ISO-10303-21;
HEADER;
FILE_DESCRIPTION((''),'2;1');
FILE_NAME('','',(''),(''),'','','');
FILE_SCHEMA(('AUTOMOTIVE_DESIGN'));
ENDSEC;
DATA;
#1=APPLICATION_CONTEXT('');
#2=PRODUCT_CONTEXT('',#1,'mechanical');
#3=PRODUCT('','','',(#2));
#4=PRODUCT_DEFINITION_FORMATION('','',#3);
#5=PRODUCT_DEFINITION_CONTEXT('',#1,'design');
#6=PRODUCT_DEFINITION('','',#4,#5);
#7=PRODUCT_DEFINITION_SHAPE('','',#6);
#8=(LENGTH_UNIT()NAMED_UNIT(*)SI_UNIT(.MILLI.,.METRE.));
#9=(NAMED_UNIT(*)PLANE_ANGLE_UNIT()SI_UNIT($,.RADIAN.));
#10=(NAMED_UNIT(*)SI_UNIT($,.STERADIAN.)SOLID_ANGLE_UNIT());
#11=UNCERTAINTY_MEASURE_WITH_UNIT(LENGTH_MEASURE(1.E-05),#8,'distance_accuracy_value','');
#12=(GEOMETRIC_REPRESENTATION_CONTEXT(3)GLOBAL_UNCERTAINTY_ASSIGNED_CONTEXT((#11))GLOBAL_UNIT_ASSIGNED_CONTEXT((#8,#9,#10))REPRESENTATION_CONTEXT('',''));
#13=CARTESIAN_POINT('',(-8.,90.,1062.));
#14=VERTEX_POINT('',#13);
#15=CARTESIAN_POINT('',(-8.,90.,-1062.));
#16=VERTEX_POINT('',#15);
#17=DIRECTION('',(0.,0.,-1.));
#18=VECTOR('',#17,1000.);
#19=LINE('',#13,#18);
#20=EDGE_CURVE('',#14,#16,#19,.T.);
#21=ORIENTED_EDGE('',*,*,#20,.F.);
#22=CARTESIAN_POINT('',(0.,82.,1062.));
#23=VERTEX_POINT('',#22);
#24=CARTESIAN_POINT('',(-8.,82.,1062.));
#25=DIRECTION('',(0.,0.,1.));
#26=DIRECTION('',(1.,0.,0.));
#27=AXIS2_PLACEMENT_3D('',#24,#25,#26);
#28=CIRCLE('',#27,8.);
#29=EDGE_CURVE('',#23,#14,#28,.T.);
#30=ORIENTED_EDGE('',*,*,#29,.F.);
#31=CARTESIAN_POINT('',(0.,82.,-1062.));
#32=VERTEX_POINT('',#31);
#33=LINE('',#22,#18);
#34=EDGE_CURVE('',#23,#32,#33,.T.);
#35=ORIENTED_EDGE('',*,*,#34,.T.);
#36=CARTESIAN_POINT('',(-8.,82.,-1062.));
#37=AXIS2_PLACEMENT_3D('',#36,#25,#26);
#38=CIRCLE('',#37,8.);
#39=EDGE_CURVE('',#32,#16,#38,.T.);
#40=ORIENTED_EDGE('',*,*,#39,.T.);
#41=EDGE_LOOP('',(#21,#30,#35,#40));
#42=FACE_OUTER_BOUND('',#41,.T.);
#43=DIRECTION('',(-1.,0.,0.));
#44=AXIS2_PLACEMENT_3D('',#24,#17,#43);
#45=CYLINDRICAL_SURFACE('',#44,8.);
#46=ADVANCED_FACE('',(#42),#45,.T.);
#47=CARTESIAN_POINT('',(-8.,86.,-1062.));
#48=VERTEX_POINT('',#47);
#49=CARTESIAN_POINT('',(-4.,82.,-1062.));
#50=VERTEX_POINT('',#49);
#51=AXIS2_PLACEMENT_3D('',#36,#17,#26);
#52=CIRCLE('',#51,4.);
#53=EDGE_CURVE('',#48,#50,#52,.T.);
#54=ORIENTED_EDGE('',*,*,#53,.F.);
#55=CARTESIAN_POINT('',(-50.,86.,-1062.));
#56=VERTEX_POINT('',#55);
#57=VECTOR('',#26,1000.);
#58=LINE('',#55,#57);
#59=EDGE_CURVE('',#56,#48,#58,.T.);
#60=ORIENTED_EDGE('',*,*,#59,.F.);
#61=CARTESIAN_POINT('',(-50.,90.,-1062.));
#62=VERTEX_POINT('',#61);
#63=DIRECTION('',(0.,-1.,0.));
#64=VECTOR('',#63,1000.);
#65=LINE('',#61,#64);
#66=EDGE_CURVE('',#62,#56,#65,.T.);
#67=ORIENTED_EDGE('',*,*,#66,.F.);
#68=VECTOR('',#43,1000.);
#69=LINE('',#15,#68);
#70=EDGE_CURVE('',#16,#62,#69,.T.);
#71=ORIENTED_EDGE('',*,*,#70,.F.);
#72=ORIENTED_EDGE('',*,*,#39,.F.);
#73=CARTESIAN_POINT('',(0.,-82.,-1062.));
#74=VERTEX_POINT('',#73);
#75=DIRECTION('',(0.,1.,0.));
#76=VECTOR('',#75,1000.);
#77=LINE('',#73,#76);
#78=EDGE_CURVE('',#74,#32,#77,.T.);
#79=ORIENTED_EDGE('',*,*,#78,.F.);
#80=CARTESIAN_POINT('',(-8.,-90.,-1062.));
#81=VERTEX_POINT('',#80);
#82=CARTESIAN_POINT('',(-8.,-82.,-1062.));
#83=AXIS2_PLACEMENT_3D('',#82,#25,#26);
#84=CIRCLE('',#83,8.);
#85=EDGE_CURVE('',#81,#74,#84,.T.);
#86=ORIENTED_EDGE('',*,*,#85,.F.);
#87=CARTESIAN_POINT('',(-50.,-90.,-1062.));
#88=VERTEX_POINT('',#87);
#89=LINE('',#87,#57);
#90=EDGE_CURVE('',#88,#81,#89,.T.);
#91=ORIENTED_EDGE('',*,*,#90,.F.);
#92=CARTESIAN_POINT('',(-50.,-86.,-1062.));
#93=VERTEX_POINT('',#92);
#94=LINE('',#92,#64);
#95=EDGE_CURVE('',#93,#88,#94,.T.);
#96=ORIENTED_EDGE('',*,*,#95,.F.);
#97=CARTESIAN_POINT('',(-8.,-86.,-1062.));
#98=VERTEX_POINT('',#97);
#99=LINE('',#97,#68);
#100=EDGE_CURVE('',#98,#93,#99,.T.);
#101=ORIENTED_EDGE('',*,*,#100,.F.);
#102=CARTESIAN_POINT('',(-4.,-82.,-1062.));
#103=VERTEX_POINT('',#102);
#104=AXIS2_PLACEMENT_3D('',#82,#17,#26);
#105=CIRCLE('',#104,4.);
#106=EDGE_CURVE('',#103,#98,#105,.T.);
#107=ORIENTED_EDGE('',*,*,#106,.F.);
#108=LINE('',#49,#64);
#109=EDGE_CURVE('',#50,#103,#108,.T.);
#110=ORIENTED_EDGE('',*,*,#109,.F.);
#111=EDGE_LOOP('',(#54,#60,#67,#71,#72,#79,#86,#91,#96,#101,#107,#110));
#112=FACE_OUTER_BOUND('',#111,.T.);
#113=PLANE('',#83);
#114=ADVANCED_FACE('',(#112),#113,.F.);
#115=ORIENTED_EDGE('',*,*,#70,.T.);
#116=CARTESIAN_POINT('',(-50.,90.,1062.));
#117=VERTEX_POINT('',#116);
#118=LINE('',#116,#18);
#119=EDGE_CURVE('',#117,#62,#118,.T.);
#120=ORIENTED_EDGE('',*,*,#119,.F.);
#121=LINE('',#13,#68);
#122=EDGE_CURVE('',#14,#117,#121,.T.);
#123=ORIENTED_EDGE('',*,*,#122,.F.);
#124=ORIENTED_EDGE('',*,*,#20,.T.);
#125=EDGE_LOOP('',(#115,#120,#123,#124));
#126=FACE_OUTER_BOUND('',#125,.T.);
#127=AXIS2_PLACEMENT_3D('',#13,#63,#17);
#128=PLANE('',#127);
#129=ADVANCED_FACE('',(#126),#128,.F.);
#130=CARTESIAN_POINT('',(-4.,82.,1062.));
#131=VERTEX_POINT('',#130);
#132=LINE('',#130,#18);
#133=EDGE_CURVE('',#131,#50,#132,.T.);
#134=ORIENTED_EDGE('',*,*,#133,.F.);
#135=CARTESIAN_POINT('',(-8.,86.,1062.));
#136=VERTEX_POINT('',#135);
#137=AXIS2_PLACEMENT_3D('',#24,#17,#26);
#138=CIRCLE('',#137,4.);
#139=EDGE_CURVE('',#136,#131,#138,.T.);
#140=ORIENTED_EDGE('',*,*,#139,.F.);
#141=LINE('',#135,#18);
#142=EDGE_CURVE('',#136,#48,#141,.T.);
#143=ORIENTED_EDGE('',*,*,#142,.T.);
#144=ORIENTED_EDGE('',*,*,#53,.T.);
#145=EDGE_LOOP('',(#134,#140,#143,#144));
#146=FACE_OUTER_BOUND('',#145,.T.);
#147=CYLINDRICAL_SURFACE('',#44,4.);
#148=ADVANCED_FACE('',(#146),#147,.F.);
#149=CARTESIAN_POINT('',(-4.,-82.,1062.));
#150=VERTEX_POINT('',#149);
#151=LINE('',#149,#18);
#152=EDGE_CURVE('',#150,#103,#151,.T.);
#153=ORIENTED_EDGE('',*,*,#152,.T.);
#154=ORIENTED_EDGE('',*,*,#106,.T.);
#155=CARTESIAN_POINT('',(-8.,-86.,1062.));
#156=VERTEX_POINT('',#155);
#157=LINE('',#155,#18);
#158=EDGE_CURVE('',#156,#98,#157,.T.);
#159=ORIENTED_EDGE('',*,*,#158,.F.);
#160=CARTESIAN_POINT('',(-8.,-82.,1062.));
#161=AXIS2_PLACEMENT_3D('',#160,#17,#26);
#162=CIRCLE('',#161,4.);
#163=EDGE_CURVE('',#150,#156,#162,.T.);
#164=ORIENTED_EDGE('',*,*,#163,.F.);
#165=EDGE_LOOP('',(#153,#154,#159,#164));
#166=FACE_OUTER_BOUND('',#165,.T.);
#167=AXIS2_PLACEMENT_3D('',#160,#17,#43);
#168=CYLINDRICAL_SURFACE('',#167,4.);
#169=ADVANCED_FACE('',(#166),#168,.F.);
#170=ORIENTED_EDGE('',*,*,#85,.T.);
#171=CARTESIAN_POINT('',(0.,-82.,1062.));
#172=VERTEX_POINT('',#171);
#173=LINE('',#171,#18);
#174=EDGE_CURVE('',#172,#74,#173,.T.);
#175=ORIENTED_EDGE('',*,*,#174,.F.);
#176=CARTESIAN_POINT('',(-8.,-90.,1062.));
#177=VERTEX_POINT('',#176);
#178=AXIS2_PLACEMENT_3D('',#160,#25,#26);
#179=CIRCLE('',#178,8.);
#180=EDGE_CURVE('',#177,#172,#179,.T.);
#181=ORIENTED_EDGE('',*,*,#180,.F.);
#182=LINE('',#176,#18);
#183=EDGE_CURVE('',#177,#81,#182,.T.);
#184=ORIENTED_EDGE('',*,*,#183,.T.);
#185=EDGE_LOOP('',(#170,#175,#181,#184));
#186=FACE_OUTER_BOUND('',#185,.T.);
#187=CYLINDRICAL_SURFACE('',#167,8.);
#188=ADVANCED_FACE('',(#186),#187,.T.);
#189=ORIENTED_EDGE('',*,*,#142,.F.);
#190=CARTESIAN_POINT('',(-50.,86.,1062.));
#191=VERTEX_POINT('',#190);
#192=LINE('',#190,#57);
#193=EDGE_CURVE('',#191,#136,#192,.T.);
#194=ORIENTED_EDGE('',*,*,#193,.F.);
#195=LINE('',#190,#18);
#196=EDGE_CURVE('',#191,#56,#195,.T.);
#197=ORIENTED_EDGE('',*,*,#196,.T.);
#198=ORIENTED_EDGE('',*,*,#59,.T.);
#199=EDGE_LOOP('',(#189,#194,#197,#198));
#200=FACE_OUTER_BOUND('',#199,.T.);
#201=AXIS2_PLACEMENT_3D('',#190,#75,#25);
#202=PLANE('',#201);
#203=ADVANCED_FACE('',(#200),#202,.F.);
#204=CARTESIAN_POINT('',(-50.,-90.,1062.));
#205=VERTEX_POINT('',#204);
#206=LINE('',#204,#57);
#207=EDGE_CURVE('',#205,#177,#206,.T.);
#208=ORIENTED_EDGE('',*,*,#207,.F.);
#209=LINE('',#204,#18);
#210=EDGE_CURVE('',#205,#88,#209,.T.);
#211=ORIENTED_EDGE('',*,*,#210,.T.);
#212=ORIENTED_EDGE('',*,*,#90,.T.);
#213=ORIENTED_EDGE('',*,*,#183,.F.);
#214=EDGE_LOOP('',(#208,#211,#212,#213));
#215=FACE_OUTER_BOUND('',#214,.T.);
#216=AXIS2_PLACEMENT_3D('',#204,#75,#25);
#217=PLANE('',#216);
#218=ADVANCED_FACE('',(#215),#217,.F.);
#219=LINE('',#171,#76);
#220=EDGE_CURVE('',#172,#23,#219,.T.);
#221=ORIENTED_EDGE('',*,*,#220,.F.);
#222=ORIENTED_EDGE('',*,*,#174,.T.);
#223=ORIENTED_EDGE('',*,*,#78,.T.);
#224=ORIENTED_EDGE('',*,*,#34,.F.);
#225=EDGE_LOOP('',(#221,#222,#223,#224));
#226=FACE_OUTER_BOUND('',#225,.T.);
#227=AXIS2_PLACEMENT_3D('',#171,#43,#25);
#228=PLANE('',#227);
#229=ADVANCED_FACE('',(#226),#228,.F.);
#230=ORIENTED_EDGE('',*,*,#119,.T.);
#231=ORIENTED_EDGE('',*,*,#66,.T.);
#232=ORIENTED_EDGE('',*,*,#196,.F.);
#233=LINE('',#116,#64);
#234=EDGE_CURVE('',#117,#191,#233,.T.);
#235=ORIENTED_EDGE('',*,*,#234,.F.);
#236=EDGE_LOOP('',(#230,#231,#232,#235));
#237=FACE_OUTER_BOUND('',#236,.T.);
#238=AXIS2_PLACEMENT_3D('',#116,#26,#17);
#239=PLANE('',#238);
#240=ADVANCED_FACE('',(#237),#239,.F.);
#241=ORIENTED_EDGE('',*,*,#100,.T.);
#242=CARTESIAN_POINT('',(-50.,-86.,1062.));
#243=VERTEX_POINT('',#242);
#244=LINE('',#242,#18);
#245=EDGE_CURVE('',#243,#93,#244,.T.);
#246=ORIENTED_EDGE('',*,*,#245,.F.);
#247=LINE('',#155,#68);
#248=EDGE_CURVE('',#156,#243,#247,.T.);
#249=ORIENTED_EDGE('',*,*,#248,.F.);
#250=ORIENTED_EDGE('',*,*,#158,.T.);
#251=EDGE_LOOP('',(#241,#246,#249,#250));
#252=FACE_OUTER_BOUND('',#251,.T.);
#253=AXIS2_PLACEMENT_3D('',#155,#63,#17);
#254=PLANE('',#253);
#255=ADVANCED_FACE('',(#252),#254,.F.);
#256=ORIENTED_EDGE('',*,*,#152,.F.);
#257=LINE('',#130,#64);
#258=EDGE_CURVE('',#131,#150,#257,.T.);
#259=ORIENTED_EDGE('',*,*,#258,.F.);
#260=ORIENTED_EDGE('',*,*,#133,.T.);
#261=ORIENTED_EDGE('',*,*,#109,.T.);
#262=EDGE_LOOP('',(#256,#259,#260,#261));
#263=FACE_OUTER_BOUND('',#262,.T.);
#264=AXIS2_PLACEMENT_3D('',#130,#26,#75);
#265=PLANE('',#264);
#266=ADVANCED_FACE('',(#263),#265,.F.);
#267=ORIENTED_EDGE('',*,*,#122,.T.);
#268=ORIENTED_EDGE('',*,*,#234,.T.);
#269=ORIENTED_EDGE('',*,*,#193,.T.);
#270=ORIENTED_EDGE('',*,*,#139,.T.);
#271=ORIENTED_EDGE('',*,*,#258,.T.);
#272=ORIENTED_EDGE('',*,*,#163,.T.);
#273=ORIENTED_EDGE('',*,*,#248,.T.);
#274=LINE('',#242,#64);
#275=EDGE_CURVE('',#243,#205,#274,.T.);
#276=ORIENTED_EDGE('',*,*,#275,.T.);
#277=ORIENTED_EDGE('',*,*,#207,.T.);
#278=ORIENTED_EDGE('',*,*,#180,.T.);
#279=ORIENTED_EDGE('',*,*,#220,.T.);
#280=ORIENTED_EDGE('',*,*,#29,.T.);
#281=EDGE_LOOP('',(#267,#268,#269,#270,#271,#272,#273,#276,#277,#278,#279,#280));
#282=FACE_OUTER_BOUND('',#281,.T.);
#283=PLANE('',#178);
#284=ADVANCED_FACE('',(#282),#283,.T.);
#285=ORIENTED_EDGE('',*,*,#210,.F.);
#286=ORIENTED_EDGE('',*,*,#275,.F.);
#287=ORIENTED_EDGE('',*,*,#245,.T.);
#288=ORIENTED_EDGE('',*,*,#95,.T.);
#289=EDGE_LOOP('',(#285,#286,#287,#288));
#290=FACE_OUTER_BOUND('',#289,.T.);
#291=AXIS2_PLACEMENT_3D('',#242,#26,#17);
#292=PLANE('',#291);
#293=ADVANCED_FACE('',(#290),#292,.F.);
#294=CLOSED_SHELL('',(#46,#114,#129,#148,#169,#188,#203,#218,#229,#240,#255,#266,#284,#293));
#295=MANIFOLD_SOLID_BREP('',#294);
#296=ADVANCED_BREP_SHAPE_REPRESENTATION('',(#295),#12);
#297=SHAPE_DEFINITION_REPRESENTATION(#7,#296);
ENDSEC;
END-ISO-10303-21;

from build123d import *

# Parameters (mm, degrees)
BOSS_EXTRUDE1_DEPTH = 1062


with BuildPart() as part:
    # Sketch1 → Boss-Extrude1 (new, symmetric)
    with BuildSketch(Plane.XY):
        with BuildLine():
            Line((-50, -90), (-8, -90))
            ThreePointArc((-8, -90), (-2.343145751, -87.656854249), (0, -82))
            Line((0, -82), (0, 82))
            ThreePointArc((0, 82), (-2.343145751, 87.656854249), (-8, 90))
            Line((-8, 90), (-50, 90))
            Line((-50, 90), (-50, 86))
            Line((-50, 86), (-8, 86))
            ThreePointArc((-8, 86), (-5.171572875, 84.828427125), (-4, 82))
            Line((-4, 82), (-4, -82))
            ThreePointArc((-4, -82), (-5.171572875, -84.828427125), (-8, -86))
            Line((-8, -86), (-50, -86))
            Line((-50, -86), (-50, -90))
        make_face()
    extrude(amount=BOSS_EXTRUDE1_DEPTH, both=True)


solid = part.part
